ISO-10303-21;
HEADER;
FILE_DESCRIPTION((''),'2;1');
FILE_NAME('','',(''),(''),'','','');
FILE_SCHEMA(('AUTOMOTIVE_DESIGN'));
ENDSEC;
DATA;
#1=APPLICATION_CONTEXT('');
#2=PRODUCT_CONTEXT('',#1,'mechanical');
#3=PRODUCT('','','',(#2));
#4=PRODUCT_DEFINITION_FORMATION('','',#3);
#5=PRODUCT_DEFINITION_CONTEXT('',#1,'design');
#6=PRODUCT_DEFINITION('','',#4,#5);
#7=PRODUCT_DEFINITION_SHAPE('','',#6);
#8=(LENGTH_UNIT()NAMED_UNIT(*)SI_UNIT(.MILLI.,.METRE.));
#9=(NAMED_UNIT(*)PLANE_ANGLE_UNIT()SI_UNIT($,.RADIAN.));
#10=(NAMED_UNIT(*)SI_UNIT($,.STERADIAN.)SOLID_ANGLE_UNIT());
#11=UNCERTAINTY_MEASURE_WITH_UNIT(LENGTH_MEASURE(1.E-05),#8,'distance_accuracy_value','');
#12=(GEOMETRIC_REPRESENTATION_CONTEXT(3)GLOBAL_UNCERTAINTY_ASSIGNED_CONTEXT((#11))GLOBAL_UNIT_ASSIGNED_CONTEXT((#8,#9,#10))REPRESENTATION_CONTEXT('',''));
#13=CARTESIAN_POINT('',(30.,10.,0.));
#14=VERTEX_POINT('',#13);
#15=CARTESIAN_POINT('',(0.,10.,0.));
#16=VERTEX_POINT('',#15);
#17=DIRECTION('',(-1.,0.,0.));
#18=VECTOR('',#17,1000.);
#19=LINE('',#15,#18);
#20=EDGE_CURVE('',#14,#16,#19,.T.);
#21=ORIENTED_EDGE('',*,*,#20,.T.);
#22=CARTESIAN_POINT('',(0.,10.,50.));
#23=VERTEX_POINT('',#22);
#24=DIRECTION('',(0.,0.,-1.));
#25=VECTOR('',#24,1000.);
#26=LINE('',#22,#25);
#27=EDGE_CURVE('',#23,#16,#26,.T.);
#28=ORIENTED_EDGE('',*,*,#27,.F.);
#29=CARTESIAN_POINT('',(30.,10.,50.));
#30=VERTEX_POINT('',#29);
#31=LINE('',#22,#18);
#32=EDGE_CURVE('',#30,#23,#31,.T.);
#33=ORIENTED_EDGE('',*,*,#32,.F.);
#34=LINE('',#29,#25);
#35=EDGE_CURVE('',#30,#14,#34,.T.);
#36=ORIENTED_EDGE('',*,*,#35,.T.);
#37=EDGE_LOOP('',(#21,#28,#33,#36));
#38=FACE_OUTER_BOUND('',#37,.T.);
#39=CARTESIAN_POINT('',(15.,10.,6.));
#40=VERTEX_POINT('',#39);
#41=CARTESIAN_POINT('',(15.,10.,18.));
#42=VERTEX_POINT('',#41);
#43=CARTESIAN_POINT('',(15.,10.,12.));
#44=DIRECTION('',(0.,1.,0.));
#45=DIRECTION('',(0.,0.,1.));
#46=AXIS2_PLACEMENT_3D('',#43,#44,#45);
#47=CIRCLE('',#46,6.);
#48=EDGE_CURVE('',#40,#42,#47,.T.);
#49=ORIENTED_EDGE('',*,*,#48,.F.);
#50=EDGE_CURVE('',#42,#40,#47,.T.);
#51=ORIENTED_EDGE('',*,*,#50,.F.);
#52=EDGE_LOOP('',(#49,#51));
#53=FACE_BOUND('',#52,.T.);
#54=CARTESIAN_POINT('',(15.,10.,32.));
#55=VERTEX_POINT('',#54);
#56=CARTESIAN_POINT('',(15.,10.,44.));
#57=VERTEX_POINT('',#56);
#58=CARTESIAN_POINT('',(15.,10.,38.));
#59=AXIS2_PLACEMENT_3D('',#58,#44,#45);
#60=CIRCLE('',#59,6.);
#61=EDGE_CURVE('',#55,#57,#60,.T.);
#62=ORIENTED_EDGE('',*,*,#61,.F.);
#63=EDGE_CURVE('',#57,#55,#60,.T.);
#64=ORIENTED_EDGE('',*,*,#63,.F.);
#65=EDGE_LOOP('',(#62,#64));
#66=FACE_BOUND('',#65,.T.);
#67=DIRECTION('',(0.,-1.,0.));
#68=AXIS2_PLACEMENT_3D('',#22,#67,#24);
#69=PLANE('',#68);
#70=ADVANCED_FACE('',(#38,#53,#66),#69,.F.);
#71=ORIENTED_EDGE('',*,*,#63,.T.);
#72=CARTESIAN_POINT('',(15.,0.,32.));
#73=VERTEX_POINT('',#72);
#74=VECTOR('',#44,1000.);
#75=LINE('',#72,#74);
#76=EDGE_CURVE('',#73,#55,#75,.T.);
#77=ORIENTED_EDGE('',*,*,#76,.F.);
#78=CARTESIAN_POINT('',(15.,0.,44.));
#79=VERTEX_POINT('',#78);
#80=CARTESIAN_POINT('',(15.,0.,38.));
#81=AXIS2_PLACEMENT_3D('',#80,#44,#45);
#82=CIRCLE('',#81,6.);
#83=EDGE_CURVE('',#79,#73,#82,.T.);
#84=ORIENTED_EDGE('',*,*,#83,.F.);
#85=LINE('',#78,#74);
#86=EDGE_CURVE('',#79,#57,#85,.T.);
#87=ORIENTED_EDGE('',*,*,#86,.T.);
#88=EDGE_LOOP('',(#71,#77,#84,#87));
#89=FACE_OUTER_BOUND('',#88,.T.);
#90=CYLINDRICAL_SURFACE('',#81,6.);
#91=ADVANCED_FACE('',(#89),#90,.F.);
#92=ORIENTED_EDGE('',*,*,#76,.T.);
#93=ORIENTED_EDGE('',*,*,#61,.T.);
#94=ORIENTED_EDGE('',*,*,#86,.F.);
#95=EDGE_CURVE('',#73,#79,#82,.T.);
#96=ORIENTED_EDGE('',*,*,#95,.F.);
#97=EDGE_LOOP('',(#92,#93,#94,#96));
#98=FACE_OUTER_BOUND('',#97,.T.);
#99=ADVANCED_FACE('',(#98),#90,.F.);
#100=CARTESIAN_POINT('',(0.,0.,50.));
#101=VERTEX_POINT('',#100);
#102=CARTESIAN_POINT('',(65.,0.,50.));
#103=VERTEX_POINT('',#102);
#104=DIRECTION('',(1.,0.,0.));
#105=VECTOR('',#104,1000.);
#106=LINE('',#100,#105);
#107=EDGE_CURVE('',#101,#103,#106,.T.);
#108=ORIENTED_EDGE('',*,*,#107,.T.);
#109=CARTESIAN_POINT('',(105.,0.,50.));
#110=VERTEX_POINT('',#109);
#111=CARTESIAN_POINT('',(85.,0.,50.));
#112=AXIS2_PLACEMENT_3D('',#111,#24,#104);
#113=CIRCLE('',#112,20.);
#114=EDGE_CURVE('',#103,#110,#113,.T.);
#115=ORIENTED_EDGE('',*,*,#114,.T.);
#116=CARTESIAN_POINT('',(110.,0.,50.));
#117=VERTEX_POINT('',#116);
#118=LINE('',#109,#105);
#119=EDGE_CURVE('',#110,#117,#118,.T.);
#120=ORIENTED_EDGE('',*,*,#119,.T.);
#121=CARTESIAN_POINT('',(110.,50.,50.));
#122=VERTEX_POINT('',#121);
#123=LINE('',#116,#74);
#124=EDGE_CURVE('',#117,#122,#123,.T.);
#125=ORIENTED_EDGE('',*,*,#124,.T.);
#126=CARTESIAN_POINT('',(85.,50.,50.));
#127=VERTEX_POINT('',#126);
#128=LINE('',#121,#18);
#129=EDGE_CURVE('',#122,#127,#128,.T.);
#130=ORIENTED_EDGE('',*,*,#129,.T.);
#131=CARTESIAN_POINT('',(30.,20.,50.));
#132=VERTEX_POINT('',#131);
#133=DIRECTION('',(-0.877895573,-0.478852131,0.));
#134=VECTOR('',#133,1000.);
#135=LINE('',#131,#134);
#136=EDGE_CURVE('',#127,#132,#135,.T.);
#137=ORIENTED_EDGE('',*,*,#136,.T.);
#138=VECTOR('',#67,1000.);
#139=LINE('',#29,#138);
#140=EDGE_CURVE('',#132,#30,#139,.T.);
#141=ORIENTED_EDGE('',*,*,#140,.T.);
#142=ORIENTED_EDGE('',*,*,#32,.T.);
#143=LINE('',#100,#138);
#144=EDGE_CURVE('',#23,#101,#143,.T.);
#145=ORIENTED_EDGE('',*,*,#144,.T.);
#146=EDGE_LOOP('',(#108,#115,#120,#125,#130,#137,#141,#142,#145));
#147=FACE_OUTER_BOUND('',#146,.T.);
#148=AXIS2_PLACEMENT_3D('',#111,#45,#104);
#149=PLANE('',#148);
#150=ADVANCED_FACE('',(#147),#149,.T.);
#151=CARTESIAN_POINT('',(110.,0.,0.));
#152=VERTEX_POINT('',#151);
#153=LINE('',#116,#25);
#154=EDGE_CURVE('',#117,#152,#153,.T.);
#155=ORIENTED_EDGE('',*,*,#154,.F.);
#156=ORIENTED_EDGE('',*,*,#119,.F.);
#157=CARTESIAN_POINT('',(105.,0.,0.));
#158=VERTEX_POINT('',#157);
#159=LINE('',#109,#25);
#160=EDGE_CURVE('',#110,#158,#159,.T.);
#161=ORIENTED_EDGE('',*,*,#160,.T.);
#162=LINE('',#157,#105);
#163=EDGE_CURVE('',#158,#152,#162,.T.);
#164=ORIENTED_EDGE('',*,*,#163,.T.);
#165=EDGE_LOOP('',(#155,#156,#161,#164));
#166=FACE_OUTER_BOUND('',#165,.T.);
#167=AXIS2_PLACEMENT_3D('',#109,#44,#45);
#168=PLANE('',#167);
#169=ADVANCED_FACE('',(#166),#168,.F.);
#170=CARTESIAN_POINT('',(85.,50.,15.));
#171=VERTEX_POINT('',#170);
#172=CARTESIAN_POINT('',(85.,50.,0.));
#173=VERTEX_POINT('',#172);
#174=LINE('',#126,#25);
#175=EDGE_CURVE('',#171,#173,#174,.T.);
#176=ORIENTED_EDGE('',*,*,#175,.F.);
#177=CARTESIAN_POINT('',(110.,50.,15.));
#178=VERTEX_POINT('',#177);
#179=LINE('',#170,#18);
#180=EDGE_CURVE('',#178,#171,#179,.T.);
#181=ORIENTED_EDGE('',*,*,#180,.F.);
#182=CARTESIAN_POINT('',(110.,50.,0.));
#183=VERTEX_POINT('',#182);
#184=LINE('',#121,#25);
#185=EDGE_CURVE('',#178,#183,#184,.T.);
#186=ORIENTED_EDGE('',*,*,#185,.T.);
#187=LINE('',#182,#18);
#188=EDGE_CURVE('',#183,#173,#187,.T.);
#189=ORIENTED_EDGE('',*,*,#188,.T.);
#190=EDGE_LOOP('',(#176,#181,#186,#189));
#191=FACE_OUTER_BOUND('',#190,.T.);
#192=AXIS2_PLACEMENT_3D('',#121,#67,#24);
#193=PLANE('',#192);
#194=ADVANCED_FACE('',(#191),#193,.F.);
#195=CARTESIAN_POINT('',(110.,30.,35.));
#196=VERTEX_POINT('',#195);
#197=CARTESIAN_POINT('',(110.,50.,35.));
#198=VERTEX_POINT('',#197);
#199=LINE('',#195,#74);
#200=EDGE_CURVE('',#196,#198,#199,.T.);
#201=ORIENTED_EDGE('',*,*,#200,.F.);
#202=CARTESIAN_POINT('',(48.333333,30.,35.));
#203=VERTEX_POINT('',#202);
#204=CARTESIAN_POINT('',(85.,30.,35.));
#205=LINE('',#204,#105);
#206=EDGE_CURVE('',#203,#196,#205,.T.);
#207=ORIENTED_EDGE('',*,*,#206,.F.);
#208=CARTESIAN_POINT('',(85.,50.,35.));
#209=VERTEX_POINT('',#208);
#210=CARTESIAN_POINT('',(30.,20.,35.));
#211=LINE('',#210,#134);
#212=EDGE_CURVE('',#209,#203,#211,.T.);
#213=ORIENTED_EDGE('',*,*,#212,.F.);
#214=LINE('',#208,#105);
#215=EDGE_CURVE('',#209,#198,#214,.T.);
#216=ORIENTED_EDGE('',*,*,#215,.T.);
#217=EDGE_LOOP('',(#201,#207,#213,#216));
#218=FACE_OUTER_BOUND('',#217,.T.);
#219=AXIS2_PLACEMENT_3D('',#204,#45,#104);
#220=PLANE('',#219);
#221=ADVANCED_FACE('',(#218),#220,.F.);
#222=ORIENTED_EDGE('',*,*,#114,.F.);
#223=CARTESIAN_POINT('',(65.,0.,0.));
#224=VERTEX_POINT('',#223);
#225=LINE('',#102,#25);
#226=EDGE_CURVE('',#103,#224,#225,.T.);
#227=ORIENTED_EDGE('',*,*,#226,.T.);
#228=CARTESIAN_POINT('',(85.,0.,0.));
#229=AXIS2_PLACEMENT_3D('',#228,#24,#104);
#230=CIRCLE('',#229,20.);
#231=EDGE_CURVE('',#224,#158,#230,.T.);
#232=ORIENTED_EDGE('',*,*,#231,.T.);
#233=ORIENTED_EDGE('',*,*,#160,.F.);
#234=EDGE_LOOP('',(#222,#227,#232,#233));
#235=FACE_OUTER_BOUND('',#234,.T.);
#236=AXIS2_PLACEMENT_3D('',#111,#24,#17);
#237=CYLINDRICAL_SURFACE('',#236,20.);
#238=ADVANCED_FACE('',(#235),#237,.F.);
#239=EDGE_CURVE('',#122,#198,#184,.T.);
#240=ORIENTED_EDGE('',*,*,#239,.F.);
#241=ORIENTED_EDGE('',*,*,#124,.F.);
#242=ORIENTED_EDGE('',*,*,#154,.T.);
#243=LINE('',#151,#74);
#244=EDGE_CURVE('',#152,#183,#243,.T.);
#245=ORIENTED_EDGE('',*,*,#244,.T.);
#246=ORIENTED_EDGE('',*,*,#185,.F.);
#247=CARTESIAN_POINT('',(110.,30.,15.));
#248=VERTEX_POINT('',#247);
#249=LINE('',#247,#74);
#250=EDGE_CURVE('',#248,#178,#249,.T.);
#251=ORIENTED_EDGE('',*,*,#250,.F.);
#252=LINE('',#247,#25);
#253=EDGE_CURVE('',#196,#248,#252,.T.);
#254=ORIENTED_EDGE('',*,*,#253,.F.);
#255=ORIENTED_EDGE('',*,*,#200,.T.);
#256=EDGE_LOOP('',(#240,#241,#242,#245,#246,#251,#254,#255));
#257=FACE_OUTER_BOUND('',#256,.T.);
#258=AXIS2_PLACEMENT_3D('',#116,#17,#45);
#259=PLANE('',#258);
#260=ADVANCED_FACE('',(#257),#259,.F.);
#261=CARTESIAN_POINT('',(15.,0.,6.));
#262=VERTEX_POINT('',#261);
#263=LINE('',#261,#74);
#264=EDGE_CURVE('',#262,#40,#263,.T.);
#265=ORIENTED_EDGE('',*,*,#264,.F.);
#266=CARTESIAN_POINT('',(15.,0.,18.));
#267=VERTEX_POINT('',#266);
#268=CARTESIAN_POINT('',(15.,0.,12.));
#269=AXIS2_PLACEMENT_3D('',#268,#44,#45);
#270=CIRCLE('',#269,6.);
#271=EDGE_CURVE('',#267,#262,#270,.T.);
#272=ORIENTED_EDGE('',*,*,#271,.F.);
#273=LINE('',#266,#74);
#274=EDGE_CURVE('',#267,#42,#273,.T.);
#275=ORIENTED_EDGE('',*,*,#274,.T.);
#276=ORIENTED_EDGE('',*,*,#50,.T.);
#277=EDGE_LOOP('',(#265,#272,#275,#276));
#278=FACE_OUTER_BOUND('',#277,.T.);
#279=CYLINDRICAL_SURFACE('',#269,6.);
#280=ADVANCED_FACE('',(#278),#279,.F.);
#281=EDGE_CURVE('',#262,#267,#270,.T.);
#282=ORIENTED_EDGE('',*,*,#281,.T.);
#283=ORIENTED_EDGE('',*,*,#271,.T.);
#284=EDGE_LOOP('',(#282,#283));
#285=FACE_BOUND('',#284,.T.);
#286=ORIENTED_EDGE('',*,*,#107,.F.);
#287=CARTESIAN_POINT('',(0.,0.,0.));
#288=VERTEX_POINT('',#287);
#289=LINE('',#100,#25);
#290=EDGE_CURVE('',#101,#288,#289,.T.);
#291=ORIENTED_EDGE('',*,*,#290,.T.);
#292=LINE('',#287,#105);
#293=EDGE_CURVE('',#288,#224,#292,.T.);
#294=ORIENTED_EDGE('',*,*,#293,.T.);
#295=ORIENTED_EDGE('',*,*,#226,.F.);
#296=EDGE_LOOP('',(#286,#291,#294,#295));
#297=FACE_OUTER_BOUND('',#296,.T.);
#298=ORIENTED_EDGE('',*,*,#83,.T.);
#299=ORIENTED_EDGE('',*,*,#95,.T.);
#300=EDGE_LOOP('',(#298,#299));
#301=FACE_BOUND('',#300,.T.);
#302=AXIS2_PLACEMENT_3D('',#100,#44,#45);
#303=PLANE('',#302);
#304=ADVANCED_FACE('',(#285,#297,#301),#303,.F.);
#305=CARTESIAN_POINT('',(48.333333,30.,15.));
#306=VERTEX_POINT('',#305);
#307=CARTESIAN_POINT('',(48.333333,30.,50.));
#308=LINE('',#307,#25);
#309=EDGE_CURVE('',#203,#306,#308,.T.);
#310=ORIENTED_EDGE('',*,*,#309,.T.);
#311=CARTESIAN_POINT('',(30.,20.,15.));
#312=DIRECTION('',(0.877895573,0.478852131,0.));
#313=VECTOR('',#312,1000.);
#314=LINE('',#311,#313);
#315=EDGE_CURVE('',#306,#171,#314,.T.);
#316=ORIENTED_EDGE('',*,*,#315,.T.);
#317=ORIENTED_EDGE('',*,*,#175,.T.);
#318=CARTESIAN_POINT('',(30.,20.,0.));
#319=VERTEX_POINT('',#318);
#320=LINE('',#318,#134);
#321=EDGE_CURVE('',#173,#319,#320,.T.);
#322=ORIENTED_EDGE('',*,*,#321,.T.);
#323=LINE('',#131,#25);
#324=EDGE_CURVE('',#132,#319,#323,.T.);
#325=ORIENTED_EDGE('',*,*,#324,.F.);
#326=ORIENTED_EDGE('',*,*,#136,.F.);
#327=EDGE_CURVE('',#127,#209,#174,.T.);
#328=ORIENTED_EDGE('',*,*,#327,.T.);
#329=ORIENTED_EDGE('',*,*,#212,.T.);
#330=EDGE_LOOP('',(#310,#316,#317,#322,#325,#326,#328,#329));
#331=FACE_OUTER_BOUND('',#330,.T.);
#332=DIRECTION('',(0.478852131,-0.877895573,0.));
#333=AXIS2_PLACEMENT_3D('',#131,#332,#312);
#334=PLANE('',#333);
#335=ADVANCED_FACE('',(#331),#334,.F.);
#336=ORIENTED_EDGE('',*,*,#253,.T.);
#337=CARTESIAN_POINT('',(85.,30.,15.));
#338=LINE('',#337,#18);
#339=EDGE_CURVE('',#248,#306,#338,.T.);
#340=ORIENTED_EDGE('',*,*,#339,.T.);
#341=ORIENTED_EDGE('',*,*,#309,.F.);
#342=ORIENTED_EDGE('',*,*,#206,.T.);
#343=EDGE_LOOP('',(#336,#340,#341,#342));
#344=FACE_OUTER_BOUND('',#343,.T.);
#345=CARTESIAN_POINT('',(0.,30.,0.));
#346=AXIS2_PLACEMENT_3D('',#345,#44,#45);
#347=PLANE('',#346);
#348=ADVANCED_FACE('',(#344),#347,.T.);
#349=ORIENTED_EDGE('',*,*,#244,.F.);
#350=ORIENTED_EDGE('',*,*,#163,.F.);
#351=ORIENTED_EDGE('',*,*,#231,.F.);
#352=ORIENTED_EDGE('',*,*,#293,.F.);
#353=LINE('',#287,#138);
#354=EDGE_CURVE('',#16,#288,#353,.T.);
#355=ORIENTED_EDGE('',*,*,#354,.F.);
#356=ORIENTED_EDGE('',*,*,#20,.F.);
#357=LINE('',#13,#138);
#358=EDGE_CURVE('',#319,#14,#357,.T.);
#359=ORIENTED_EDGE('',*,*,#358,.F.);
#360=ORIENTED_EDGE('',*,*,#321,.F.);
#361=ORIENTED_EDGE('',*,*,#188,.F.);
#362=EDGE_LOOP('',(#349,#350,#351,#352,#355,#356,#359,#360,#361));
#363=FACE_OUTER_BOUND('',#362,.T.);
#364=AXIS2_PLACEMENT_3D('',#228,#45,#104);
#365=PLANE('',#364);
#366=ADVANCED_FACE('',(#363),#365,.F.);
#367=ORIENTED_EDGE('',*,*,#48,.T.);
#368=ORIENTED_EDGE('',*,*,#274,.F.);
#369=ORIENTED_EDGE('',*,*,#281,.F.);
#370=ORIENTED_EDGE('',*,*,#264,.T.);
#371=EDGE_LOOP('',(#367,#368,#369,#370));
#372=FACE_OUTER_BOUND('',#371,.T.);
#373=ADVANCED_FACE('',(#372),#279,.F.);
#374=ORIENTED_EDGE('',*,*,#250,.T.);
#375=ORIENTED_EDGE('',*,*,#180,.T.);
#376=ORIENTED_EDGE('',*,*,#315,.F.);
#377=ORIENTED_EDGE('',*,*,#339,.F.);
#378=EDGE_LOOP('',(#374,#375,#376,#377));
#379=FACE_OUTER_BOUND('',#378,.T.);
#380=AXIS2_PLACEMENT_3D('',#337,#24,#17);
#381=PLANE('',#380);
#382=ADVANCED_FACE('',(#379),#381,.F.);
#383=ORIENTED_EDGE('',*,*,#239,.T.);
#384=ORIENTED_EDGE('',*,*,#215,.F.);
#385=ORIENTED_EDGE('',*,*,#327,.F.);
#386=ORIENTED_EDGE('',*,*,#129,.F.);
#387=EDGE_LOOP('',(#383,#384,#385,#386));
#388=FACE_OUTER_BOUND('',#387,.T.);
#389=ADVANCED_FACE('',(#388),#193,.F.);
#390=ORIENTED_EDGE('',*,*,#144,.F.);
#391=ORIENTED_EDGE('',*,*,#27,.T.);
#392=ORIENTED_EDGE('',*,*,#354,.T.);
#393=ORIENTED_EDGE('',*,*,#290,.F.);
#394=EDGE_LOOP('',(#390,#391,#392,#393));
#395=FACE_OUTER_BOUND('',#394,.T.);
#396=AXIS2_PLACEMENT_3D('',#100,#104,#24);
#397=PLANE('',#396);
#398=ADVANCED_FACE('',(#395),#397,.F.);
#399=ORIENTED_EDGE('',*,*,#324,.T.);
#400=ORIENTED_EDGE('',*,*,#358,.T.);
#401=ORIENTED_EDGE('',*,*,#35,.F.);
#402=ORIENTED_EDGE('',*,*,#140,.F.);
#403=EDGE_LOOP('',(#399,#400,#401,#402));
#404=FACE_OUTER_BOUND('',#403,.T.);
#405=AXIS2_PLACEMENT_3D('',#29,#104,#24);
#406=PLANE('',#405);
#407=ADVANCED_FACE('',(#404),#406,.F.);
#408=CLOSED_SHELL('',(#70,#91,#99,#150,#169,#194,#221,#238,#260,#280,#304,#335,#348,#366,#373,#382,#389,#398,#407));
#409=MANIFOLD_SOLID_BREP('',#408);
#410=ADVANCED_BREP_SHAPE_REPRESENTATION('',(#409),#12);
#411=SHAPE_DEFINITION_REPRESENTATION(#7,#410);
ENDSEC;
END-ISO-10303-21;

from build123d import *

# Parameters (mm, degrees)
BRACKET_BODY_DEPTH      = 50
TOP_GROOVE_SKETCH_W     = 25
TOP_GROOVE_SKETCH_H     = 20
TOP_GROOVE_CUT_DEPTH    = 20
NOTCH_SKETCH_W          = 20
NOTCH_SKETCH_H          = 20
NOTCH_CUT_DEPTH         = 111.566721937
MOUNTING_HOLES_SKETCH_R = 6
MOUNTING_HOLES_2X_DEPTH = 128.279220614


with BuildPart() as part:
    # Bracket Profile Sketch → Bracket Body (new body)
    with BuildSketch(Plane.XY):
        with BuildLine():
            Line((0, 0), (65, 0))
            ThreePointArc((65, 0), (85, 20), (105, 0))
            Line((105, 0), (110, 0))
            Line((110, 0), (110, 50))
            Line((110, 50), (85, 50))
            Line((85, 50), (30, 20))
            Line((30, 20), (30, 10))
            Line((30, 10), (0, 10))
            Line((0, 10), (0, 0))
        make_face()
    extrude(amount=BRACKET_BODY_DEPTH)

    # Top Groove Sketch → Top Groove Cut (cut)
    with BuildSketch(Plane(origin=(0, 50, 0), x_dir=(1, 0, 0), z_dir=(0, 1, 0))):
        with Locations((97.5, -25)):
            Rectangle(TOP_GROOVE_SKETCH_W, TOP_GROOVE_SKETCH_H)
    extrude(amount=-TOP_GROOVE_CUT_DEPTH, mode=Mode.SUBTRACT)

    # Notch Sketch → Notch Cut (cut, through all)
    with BuildSketch(Plane(origin=(85, 0, 0), x_dir=(0, 0, -1), z_dir=(1, 0, 0))):
        with Locations((-25, 40)):
            Rectangle(NOTCH_SKETCH_W, NOTCH_SKETCH_H)
    extrude(amount=-NOTCH_CUT_DEPTH, mode=Mode.SUBTRACT)

    # Mounting Holes Sketch → Mounting Holes 2x (cut, through all)
    with BuildSketch(Plane(origin=(0, 10, 0), x_dir=(1, 0, 0), z_dir=(0, 1, 0))):
        with Locations(Location((15, -12, 0), (0, 0, 270))):
            Circle(MOUNTING_HOLES_SKETCH_R)
        with Locations(Location((15, -38, 0), (0, 0, 270))):
            Circle(MOUNTING_HOLES_SKETCH_R)
    extrude(amount=-MOUNTING_HOLES_2X_DEPTH, mode=Mode.SUBTRACT)


solid = part.part
